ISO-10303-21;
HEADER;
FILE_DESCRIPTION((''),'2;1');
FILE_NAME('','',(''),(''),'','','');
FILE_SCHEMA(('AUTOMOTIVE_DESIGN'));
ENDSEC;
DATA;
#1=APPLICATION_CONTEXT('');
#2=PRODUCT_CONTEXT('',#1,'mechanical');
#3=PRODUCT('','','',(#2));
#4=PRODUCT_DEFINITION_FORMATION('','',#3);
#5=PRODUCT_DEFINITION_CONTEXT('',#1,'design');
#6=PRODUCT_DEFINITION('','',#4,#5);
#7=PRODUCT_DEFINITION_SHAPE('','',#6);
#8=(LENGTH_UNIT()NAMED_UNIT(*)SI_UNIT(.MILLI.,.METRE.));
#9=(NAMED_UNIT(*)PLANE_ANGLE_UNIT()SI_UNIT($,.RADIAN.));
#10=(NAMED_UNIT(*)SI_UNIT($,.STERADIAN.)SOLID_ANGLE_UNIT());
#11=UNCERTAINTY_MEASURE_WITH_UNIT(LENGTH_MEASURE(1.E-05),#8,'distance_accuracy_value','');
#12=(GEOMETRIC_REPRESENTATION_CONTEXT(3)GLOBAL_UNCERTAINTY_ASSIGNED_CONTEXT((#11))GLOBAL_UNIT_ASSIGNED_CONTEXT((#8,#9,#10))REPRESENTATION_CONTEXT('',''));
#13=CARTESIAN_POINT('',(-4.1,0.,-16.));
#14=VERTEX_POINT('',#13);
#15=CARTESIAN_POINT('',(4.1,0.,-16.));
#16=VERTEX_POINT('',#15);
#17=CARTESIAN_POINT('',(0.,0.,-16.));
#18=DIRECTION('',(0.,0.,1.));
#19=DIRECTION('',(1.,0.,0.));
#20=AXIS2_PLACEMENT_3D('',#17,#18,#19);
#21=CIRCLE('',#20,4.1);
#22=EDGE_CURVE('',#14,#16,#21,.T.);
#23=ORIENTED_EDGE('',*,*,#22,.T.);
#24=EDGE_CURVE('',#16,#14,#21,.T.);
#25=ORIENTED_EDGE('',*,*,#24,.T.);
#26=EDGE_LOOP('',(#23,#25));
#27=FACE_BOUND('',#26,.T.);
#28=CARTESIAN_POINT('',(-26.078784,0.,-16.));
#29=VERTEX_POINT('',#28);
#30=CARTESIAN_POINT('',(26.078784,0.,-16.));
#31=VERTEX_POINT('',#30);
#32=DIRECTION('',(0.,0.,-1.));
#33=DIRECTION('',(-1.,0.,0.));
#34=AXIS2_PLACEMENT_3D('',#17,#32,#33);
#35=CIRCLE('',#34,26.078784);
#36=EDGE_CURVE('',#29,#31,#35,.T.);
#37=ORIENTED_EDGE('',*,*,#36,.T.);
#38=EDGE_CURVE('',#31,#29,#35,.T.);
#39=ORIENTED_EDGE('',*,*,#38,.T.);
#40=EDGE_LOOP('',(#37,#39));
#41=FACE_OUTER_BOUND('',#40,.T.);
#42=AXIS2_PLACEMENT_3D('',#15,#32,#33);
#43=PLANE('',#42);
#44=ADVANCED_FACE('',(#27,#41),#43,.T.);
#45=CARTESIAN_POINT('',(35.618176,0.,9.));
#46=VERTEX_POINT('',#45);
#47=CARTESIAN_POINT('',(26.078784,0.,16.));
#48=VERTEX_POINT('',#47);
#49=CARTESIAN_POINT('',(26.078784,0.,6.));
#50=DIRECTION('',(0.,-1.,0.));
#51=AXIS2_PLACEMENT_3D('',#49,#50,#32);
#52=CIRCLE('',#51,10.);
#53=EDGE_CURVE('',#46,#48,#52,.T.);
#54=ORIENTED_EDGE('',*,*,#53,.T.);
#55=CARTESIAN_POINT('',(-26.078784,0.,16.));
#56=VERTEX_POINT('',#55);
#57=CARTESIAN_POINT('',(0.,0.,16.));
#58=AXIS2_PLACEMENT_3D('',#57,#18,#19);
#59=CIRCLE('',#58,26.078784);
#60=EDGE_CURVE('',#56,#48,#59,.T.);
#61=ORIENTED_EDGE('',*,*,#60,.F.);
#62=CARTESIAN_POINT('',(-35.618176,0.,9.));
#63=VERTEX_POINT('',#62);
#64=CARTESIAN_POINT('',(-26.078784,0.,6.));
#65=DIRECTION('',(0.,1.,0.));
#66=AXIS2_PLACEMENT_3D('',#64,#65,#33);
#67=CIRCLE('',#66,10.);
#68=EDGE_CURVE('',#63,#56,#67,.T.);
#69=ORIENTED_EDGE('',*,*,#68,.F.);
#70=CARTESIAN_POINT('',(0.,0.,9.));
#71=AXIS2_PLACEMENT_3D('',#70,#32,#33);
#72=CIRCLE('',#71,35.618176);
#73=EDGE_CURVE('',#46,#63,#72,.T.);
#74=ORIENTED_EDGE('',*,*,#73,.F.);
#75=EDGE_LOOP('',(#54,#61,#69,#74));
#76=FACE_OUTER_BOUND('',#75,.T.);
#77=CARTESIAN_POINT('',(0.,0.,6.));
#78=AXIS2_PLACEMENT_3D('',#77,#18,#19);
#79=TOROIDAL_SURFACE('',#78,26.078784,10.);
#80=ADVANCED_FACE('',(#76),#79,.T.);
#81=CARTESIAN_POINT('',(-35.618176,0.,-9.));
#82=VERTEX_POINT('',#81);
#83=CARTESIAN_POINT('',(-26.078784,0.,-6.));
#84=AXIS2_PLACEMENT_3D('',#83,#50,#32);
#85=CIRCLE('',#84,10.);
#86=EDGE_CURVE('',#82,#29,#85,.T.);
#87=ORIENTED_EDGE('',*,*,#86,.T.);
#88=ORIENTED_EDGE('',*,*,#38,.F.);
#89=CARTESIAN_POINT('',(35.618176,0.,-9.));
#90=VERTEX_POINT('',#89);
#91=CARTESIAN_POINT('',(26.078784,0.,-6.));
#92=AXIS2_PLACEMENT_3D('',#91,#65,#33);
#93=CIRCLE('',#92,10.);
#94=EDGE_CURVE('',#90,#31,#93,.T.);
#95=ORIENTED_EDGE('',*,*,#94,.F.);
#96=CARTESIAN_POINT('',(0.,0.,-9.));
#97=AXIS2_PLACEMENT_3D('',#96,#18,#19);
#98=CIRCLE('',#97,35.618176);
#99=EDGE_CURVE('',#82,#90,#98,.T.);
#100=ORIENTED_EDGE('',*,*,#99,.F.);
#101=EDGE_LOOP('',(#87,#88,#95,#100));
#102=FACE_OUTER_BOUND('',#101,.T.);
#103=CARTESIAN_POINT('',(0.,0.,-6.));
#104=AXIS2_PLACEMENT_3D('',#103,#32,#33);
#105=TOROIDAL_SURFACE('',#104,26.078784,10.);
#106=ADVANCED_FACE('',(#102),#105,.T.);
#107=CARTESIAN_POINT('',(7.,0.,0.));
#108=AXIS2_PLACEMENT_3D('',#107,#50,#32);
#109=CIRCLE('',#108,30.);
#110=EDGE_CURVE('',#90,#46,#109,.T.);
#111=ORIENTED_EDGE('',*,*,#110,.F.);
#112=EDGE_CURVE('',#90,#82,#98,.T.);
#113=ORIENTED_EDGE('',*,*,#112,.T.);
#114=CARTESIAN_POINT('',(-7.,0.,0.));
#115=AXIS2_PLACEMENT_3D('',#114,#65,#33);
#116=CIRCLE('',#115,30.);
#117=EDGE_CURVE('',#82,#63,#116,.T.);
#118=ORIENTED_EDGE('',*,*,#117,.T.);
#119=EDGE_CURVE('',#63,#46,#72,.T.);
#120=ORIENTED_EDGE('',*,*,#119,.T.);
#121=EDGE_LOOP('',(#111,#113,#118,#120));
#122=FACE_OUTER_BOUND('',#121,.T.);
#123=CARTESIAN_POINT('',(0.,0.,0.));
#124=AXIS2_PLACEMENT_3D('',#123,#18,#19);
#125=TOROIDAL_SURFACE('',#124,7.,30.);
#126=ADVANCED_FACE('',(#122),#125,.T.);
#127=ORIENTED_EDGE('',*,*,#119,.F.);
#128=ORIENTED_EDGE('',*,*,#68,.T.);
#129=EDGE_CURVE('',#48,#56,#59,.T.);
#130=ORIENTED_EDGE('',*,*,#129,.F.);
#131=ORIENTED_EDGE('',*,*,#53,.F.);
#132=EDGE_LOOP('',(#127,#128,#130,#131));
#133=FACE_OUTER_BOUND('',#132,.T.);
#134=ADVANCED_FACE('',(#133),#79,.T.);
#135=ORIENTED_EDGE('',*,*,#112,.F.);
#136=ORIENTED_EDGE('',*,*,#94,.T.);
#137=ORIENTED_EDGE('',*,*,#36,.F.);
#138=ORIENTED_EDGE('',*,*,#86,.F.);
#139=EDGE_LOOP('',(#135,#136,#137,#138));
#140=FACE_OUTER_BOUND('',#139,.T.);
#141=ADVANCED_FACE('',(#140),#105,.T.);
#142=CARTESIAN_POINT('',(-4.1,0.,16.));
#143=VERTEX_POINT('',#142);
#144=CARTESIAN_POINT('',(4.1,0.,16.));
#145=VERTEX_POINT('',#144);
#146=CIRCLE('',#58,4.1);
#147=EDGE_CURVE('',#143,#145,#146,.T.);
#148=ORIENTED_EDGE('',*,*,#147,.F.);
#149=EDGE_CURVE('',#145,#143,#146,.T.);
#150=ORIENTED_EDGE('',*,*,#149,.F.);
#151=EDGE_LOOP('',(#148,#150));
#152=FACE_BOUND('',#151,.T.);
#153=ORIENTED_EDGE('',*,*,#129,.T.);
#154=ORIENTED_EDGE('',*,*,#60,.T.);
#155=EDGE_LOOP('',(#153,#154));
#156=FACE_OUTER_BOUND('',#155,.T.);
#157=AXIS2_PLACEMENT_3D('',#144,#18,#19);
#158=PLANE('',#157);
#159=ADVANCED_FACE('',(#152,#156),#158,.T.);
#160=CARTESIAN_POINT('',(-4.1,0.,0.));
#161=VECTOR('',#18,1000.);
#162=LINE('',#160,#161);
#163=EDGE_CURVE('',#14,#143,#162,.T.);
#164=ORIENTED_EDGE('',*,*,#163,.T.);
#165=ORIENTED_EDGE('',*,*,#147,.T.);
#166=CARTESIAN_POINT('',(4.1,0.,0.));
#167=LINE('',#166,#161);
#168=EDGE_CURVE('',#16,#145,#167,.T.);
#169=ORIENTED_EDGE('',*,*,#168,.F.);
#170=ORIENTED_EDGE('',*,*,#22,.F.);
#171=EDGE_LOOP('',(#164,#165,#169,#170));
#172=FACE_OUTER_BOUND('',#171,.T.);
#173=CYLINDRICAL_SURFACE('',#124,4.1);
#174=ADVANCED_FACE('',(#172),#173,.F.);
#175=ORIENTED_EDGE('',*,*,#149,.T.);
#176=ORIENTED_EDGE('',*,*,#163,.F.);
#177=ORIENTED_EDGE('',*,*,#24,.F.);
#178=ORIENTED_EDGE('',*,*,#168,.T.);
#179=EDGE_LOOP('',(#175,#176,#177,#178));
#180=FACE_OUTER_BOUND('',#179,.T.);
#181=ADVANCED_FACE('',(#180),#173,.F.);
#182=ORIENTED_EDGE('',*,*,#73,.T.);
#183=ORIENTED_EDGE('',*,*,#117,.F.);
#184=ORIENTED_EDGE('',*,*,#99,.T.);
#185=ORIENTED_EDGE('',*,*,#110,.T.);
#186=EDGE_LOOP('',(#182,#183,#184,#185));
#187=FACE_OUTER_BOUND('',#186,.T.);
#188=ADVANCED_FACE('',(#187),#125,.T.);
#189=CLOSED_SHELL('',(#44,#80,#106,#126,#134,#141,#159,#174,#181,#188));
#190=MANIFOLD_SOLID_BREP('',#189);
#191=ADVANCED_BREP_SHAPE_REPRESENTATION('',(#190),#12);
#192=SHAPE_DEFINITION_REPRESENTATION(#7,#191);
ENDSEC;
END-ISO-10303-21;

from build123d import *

# Parameters (mm, degrees)
FILLET_1_R = 10


with BuildPart() as part:
    # 草图1 → 旋转1 (revolve)
    with BuildSketch(Plane(origin=(0, 0, 0), x_dir=(1, 0, 0), z_dir=(0, 1, 0))):
        with BuildLine():
            Line((4.1, 16), (32.377155081, 16))
            ThreePointArc((32.377155081, 16), (37, 0), (32.377155081, -16))
            Line((32.377155081, -16), (4.1, -16))
            Line((4.1, -16), (4.1, 16))
        make_face()
    revolve(axis=Axis((0, 0, 0), (0, 0, -1)))

    # 圆角1
    fillet_1_edges = [part.edges().sort_by_distance(p)[0] for p in [
        (-32.377155081, 0, 16),
        (-32.377155081, 0, -16),
    ]]
    fillet(fillet_1_edges, radius=FILLET_1_R)


solid = part.part
